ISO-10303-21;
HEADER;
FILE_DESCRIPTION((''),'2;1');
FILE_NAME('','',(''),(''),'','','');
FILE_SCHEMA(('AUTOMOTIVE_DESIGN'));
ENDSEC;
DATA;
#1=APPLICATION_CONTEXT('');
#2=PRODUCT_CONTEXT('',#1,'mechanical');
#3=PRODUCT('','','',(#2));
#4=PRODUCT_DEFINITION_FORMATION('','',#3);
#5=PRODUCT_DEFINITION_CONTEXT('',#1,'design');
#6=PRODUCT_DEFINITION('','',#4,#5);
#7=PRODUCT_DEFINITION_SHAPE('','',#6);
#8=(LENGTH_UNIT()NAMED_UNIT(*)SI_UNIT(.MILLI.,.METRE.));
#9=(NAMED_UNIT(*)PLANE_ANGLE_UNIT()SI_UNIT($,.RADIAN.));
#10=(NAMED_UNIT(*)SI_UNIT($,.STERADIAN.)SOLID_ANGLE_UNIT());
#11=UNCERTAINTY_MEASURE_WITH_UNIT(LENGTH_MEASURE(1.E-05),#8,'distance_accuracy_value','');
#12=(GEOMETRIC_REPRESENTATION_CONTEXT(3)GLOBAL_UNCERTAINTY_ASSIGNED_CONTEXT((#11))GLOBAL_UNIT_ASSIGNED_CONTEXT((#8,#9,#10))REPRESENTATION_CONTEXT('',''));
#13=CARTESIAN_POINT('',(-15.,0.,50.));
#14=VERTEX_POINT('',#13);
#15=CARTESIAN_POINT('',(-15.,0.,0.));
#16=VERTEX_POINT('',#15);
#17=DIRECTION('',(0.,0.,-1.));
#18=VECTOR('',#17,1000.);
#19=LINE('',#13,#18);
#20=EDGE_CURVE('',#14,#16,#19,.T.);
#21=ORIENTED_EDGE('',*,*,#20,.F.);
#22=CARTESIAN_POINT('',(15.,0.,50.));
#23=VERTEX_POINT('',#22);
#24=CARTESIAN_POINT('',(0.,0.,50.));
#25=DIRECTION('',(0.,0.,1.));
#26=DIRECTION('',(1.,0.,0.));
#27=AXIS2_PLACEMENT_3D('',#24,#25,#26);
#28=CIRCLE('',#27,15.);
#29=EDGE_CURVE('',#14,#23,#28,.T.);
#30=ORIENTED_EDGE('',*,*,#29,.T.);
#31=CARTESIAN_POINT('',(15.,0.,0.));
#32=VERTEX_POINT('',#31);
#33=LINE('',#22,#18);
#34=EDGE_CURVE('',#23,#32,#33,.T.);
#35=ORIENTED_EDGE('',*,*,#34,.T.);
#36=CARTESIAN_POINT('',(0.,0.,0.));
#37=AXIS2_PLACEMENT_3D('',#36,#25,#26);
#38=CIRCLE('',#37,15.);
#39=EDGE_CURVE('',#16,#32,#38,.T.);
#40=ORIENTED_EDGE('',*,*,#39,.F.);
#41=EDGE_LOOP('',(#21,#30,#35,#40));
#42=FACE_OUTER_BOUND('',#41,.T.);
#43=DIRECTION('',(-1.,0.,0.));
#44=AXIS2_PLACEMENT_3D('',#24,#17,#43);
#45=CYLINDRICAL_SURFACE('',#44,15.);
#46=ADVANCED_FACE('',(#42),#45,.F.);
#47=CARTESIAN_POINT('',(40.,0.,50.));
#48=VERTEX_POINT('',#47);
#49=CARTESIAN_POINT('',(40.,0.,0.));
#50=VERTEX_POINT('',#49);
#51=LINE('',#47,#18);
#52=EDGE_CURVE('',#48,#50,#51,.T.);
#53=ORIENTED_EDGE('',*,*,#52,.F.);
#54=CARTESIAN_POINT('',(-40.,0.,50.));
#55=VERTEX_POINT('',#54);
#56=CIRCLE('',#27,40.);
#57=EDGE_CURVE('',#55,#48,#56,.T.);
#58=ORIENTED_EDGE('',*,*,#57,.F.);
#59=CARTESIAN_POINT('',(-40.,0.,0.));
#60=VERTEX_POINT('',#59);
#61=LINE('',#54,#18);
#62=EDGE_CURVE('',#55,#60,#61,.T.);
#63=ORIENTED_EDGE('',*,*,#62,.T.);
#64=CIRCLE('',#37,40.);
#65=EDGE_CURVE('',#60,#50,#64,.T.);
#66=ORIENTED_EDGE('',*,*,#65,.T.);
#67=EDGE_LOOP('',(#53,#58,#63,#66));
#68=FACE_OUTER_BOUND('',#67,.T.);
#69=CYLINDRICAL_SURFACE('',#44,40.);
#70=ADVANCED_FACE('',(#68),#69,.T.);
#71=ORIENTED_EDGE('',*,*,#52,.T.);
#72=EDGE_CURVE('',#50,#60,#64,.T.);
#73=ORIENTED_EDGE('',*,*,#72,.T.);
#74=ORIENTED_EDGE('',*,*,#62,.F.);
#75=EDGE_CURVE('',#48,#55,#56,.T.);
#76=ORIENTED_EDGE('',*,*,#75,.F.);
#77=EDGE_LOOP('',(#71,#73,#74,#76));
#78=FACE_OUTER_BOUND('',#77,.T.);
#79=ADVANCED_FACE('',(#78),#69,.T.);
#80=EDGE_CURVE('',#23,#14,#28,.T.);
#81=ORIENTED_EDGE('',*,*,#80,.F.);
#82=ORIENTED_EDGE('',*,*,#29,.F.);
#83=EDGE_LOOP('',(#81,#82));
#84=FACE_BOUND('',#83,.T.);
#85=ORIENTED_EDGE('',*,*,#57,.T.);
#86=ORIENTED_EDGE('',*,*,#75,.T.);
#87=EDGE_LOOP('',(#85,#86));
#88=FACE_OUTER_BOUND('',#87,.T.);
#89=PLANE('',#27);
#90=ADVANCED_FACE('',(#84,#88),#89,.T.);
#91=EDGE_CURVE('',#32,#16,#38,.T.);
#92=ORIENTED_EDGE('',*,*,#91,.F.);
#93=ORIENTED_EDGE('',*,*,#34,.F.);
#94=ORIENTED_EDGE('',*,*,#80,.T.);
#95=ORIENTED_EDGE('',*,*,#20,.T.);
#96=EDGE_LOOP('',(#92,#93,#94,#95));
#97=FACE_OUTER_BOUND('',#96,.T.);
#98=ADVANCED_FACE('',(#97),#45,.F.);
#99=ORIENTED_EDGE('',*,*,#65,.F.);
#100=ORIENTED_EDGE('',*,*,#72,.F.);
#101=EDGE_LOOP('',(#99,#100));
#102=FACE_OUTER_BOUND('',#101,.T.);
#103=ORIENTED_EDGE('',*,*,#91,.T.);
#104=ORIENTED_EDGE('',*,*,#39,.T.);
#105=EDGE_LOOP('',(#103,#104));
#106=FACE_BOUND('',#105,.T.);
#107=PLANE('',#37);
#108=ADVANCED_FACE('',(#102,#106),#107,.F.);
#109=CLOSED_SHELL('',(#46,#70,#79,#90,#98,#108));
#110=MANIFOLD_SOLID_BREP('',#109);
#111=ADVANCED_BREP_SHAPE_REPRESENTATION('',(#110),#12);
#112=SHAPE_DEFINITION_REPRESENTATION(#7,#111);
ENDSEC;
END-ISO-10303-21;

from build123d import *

# Parameters (mm, degrees)
SKETCH_1_R      = 40
SKETCH_1_R_2    = 15
EXTRUDE_1_DEPTH = 50


with BuildPart() as part:
    # 草图1 → 凸台-拉伸1 (new body)
    with BuildSketch(Plane.XY):
        Circle(SKETCH_1_R)
        Circle(SKETCH_1_R_2, mode=Mode.SUBTRACT)
    extrude(amount=EXTRUDE_1_DEPTH)


solid = part.part
